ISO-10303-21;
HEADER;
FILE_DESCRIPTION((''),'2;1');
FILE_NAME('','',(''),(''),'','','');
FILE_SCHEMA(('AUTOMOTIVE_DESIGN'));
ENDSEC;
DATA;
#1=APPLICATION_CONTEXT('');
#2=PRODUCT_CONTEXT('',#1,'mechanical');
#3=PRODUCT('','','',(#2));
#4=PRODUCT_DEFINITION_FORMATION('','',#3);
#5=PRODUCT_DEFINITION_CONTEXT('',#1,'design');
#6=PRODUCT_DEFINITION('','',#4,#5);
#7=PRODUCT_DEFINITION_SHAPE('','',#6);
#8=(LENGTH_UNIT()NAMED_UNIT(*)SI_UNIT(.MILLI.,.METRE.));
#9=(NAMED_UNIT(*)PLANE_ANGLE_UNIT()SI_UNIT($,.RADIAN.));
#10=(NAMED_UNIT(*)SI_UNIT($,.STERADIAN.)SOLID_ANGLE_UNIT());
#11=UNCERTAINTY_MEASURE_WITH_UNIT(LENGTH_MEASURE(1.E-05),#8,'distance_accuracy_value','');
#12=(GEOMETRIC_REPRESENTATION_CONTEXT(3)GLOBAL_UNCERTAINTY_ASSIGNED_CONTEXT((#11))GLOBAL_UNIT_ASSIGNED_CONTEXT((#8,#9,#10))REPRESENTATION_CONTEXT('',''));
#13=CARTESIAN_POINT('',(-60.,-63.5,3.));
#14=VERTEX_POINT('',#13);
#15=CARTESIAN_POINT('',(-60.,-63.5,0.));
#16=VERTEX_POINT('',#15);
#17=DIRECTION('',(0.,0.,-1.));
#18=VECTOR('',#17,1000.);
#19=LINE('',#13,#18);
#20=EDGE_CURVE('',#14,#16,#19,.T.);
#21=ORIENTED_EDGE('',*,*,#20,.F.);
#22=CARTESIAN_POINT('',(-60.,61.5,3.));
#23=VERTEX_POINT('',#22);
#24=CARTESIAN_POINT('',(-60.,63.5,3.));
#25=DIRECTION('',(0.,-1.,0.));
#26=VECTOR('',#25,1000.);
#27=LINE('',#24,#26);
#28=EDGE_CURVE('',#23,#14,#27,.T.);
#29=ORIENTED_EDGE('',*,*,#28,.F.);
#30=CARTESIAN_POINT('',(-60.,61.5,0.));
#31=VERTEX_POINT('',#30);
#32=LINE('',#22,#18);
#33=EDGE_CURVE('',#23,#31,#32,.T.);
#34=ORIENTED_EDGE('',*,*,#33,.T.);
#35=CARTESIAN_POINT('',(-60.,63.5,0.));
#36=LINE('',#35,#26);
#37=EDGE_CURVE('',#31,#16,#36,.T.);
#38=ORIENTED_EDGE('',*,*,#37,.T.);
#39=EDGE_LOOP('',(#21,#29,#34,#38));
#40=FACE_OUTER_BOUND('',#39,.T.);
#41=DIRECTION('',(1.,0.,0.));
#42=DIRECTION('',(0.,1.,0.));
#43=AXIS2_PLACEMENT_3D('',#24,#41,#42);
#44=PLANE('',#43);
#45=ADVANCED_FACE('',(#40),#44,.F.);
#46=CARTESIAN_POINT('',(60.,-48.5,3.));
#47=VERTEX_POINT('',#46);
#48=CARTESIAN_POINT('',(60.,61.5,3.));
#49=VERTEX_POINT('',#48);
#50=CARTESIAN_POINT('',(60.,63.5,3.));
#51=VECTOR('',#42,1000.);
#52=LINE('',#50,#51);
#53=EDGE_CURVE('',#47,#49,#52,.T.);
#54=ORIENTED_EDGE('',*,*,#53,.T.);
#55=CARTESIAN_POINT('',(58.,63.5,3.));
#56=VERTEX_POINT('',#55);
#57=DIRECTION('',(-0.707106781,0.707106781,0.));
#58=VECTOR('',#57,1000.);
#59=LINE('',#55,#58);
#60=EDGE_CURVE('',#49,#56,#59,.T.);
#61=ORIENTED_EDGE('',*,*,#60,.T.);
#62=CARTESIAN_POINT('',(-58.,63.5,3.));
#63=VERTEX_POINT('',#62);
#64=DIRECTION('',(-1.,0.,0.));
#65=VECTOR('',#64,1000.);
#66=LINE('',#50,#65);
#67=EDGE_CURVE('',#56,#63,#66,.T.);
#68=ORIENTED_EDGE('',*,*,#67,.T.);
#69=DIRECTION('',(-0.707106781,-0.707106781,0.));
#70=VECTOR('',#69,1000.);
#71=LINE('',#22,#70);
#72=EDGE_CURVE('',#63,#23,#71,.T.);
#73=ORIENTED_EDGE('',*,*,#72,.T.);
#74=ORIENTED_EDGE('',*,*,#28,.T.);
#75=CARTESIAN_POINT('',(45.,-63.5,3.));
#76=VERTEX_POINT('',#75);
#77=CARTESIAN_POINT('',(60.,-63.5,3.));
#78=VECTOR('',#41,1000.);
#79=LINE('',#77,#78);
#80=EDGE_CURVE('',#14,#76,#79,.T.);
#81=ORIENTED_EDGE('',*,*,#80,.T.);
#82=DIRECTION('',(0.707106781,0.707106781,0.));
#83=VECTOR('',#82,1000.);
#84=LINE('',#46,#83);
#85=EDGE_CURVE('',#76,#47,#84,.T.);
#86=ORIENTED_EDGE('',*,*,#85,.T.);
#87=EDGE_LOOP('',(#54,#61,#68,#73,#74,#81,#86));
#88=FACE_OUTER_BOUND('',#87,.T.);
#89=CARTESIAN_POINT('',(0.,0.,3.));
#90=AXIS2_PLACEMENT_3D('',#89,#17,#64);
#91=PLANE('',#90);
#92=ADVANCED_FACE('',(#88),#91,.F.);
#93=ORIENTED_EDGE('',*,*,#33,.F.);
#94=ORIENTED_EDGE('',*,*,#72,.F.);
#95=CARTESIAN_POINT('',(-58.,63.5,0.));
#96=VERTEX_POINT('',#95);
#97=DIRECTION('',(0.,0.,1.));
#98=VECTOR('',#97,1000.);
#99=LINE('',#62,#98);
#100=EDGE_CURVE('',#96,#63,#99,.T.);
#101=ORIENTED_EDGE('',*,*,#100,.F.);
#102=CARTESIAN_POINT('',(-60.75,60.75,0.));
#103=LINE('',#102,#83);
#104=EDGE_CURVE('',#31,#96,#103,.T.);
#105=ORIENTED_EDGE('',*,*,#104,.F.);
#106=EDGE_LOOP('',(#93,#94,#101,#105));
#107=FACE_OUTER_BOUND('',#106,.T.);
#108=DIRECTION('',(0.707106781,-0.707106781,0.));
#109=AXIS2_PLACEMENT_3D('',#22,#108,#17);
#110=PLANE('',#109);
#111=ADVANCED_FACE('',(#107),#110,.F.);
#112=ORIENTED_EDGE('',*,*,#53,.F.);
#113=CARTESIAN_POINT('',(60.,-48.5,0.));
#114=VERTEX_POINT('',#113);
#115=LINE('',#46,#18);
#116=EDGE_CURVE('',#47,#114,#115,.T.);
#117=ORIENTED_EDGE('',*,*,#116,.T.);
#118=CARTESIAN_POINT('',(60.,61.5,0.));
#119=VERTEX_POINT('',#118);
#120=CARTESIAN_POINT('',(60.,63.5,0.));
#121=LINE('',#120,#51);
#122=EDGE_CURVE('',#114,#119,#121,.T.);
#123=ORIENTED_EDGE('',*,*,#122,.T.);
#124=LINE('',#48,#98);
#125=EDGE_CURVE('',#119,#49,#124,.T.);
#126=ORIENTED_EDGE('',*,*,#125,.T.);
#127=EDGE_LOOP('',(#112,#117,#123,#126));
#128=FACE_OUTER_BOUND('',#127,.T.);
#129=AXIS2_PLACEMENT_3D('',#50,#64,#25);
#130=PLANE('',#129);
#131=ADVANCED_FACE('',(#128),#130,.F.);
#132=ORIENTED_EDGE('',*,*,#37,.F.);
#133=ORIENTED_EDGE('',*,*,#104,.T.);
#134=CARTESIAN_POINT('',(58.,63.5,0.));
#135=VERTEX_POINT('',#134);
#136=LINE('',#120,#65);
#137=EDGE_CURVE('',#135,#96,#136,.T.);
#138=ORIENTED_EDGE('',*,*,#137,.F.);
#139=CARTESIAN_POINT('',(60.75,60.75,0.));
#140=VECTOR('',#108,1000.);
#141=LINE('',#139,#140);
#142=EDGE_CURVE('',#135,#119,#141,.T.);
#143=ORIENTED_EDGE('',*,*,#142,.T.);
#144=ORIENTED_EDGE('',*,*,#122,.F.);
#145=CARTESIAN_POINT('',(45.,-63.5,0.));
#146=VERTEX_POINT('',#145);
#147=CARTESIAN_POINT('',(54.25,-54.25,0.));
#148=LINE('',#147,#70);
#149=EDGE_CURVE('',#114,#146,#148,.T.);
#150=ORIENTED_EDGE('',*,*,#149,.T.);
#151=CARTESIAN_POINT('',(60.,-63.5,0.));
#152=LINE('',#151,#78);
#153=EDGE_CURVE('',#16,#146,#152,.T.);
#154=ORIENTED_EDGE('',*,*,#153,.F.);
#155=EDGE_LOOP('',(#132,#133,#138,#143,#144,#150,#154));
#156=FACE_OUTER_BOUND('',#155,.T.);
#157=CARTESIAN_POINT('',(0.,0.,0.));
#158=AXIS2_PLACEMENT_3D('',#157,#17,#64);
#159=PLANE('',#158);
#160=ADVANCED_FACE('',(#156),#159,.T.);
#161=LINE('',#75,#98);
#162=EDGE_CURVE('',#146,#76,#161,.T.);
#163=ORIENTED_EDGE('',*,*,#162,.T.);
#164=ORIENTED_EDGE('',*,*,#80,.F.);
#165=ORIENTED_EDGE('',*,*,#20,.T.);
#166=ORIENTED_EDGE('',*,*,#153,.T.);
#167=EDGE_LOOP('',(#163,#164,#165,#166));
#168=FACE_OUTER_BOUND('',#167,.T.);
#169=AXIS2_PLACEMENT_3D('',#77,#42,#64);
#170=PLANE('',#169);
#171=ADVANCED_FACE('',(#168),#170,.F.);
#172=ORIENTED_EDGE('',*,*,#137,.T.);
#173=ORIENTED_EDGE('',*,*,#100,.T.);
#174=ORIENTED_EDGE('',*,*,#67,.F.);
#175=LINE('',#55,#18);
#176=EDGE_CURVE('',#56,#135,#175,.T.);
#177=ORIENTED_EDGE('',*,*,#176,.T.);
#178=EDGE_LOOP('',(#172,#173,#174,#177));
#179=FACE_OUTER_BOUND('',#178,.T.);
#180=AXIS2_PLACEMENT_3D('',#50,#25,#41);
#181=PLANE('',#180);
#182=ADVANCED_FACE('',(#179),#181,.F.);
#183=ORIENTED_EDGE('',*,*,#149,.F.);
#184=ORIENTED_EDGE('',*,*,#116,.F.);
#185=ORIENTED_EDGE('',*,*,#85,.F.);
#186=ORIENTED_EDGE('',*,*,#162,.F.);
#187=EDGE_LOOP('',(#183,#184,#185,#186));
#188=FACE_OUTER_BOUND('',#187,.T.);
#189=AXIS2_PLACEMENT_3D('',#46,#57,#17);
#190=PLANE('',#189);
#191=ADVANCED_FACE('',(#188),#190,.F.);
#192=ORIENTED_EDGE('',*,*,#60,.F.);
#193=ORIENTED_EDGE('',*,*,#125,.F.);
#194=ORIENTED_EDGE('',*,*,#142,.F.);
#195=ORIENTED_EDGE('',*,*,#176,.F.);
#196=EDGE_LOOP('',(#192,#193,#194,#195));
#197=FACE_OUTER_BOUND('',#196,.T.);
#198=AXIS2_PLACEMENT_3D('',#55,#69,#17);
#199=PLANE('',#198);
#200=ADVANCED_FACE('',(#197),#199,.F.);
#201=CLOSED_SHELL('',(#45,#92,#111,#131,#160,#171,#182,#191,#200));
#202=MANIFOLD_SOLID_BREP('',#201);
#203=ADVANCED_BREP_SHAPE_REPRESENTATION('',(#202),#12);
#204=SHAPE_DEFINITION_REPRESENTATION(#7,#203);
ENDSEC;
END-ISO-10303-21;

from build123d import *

# Parameters (mm, degrees)
SKETCH1_W           = 120
SKETCH1_H           = 127
BOSS_EXTRUDE1_DEPTH = 3
CHAMFER1_SIZE       = 15
CHAMFER2_SIZE       = 2


with BuildPart() as part:
    # Sketch1 → Boss-Extrude1 (new body)
    with BuildSketch(Plane.XY):
        Rectangle(SKETCH1_W, SKETCH1_H)
    extrude(amount=BOSS_EXTRUDE1_DEPTH)

    # Chamfer1
    chamfer1_edges = [part.edges().sort_by_distance(p)[0] for p in [
        (60, -63.5, 1.5),
    ]]
    chamfer(chamfer1_edges, length=CHAMFER1_SIZE)

    # Chamfer2
    chamfer2_edges = [part.edges().sort_by_distance(p)[0] for p in [
        (-60, 63.5, 1.5),
        (60, 63.5, 1.5),
    ]]
    chamfer(chamfer2_edges, length=CHAMFER2_SIZE)


solid = part.part
